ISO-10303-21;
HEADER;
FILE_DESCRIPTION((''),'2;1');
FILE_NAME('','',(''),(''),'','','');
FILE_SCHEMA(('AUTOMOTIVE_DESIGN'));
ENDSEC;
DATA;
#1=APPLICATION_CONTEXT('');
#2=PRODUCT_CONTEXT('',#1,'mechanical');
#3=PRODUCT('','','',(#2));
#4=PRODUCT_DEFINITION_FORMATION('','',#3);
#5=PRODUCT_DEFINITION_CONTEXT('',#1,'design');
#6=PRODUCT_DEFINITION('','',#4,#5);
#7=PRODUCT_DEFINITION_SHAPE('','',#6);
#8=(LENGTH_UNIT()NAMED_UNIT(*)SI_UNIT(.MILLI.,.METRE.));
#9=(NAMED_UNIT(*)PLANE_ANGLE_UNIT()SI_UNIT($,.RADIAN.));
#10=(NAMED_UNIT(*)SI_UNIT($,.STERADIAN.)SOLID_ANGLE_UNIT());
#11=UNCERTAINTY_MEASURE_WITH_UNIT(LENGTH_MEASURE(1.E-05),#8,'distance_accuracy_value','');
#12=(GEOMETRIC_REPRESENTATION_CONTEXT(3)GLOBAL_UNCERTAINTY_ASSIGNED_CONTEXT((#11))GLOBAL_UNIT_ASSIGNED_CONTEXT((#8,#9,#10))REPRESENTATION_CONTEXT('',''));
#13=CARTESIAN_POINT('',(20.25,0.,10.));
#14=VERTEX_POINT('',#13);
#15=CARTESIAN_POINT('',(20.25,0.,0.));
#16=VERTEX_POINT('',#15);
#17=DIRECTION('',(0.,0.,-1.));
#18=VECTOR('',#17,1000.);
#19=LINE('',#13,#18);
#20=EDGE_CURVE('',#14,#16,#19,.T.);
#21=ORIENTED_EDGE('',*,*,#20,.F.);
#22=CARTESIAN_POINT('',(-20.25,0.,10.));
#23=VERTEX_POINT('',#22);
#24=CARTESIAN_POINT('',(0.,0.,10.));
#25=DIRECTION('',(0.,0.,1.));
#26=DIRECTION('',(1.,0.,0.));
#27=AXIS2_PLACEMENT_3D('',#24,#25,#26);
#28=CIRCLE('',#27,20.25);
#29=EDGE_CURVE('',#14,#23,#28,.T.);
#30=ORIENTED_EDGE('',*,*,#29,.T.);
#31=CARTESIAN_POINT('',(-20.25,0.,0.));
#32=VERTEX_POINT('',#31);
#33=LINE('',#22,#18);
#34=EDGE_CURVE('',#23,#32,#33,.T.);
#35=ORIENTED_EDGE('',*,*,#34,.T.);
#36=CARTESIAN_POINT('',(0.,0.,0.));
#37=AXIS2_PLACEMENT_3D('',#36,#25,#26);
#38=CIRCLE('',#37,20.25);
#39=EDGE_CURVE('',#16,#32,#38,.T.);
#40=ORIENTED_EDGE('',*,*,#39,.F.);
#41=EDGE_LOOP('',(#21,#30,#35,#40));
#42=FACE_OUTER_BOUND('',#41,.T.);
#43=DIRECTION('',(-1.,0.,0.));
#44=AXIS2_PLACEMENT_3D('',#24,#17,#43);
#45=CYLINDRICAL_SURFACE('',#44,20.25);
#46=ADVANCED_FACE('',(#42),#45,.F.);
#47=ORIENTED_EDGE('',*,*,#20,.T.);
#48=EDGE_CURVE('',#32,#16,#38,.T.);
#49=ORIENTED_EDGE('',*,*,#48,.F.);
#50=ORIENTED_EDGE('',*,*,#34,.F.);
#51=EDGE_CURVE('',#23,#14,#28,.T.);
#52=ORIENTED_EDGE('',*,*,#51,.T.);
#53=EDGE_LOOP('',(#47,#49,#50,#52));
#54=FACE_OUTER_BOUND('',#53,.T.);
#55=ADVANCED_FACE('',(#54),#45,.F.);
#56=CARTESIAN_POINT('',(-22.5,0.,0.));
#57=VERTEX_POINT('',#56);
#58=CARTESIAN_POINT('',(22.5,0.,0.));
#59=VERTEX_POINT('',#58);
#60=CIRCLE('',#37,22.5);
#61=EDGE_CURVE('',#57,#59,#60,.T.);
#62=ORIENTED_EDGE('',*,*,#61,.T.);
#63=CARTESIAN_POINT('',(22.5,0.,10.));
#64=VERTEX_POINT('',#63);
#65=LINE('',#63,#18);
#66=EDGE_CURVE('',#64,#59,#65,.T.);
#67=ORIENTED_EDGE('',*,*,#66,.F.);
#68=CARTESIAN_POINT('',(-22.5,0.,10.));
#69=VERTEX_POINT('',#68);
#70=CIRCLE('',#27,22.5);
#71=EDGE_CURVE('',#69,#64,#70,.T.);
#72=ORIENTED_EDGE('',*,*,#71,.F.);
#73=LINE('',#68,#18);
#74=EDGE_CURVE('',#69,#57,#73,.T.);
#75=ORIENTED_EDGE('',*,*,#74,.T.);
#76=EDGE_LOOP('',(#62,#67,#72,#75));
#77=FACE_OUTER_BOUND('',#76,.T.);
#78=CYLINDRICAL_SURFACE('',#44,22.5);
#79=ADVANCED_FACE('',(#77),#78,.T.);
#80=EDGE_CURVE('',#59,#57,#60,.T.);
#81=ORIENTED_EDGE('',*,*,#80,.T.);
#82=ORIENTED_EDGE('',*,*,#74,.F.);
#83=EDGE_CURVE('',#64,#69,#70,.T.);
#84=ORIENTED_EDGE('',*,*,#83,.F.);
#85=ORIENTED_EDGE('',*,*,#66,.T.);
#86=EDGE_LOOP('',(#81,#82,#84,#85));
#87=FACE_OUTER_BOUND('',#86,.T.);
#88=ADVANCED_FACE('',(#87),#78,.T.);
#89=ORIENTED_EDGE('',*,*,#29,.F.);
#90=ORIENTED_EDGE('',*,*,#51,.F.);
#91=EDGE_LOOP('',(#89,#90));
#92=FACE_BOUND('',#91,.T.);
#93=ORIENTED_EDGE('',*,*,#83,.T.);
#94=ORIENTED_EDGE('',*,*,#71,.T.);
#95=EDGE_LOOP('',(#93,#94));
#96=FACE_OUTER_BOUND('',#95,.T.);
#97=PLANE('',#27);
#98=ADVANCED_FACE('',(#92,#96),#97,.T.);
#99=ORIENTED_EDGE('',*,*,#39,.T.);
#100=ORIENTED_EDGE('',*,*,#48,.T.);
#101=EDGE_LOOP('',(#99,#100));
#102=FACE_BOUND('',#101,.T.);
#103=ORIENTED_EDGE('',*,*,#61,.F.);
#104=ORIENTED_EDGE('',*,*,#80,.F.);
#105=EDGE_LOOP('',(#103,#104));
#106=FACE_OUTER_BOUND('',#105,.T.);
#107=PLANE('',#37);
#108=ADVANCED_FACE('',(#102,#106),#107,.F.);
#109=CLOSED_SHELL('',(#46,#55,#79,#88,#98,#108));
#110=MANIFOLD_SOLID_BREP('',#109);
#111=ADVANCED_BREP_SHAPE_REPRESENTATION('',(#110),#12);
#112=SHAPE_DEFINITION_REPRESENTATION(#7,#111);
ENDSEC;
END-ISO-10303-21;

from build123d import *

# Parameters (mm, degrees)
SKETCH_1_R      = 22.5
SKETCH_1_R_2    = 20.25
EXTRUDE_1_DEPTH = 10


with BuildPart() as part:
    # 草图1 → 凸台-拉伸1 (new body)
    with BuildSketch(Plane.XY):
        Circle(SKETCH_1_R)
        Circle(SKETCH_1_R_2, mode=Mode.SUBTRACT)
    extrude(amount=EXTRUDE_1_DEPTH)


solid = part.part
